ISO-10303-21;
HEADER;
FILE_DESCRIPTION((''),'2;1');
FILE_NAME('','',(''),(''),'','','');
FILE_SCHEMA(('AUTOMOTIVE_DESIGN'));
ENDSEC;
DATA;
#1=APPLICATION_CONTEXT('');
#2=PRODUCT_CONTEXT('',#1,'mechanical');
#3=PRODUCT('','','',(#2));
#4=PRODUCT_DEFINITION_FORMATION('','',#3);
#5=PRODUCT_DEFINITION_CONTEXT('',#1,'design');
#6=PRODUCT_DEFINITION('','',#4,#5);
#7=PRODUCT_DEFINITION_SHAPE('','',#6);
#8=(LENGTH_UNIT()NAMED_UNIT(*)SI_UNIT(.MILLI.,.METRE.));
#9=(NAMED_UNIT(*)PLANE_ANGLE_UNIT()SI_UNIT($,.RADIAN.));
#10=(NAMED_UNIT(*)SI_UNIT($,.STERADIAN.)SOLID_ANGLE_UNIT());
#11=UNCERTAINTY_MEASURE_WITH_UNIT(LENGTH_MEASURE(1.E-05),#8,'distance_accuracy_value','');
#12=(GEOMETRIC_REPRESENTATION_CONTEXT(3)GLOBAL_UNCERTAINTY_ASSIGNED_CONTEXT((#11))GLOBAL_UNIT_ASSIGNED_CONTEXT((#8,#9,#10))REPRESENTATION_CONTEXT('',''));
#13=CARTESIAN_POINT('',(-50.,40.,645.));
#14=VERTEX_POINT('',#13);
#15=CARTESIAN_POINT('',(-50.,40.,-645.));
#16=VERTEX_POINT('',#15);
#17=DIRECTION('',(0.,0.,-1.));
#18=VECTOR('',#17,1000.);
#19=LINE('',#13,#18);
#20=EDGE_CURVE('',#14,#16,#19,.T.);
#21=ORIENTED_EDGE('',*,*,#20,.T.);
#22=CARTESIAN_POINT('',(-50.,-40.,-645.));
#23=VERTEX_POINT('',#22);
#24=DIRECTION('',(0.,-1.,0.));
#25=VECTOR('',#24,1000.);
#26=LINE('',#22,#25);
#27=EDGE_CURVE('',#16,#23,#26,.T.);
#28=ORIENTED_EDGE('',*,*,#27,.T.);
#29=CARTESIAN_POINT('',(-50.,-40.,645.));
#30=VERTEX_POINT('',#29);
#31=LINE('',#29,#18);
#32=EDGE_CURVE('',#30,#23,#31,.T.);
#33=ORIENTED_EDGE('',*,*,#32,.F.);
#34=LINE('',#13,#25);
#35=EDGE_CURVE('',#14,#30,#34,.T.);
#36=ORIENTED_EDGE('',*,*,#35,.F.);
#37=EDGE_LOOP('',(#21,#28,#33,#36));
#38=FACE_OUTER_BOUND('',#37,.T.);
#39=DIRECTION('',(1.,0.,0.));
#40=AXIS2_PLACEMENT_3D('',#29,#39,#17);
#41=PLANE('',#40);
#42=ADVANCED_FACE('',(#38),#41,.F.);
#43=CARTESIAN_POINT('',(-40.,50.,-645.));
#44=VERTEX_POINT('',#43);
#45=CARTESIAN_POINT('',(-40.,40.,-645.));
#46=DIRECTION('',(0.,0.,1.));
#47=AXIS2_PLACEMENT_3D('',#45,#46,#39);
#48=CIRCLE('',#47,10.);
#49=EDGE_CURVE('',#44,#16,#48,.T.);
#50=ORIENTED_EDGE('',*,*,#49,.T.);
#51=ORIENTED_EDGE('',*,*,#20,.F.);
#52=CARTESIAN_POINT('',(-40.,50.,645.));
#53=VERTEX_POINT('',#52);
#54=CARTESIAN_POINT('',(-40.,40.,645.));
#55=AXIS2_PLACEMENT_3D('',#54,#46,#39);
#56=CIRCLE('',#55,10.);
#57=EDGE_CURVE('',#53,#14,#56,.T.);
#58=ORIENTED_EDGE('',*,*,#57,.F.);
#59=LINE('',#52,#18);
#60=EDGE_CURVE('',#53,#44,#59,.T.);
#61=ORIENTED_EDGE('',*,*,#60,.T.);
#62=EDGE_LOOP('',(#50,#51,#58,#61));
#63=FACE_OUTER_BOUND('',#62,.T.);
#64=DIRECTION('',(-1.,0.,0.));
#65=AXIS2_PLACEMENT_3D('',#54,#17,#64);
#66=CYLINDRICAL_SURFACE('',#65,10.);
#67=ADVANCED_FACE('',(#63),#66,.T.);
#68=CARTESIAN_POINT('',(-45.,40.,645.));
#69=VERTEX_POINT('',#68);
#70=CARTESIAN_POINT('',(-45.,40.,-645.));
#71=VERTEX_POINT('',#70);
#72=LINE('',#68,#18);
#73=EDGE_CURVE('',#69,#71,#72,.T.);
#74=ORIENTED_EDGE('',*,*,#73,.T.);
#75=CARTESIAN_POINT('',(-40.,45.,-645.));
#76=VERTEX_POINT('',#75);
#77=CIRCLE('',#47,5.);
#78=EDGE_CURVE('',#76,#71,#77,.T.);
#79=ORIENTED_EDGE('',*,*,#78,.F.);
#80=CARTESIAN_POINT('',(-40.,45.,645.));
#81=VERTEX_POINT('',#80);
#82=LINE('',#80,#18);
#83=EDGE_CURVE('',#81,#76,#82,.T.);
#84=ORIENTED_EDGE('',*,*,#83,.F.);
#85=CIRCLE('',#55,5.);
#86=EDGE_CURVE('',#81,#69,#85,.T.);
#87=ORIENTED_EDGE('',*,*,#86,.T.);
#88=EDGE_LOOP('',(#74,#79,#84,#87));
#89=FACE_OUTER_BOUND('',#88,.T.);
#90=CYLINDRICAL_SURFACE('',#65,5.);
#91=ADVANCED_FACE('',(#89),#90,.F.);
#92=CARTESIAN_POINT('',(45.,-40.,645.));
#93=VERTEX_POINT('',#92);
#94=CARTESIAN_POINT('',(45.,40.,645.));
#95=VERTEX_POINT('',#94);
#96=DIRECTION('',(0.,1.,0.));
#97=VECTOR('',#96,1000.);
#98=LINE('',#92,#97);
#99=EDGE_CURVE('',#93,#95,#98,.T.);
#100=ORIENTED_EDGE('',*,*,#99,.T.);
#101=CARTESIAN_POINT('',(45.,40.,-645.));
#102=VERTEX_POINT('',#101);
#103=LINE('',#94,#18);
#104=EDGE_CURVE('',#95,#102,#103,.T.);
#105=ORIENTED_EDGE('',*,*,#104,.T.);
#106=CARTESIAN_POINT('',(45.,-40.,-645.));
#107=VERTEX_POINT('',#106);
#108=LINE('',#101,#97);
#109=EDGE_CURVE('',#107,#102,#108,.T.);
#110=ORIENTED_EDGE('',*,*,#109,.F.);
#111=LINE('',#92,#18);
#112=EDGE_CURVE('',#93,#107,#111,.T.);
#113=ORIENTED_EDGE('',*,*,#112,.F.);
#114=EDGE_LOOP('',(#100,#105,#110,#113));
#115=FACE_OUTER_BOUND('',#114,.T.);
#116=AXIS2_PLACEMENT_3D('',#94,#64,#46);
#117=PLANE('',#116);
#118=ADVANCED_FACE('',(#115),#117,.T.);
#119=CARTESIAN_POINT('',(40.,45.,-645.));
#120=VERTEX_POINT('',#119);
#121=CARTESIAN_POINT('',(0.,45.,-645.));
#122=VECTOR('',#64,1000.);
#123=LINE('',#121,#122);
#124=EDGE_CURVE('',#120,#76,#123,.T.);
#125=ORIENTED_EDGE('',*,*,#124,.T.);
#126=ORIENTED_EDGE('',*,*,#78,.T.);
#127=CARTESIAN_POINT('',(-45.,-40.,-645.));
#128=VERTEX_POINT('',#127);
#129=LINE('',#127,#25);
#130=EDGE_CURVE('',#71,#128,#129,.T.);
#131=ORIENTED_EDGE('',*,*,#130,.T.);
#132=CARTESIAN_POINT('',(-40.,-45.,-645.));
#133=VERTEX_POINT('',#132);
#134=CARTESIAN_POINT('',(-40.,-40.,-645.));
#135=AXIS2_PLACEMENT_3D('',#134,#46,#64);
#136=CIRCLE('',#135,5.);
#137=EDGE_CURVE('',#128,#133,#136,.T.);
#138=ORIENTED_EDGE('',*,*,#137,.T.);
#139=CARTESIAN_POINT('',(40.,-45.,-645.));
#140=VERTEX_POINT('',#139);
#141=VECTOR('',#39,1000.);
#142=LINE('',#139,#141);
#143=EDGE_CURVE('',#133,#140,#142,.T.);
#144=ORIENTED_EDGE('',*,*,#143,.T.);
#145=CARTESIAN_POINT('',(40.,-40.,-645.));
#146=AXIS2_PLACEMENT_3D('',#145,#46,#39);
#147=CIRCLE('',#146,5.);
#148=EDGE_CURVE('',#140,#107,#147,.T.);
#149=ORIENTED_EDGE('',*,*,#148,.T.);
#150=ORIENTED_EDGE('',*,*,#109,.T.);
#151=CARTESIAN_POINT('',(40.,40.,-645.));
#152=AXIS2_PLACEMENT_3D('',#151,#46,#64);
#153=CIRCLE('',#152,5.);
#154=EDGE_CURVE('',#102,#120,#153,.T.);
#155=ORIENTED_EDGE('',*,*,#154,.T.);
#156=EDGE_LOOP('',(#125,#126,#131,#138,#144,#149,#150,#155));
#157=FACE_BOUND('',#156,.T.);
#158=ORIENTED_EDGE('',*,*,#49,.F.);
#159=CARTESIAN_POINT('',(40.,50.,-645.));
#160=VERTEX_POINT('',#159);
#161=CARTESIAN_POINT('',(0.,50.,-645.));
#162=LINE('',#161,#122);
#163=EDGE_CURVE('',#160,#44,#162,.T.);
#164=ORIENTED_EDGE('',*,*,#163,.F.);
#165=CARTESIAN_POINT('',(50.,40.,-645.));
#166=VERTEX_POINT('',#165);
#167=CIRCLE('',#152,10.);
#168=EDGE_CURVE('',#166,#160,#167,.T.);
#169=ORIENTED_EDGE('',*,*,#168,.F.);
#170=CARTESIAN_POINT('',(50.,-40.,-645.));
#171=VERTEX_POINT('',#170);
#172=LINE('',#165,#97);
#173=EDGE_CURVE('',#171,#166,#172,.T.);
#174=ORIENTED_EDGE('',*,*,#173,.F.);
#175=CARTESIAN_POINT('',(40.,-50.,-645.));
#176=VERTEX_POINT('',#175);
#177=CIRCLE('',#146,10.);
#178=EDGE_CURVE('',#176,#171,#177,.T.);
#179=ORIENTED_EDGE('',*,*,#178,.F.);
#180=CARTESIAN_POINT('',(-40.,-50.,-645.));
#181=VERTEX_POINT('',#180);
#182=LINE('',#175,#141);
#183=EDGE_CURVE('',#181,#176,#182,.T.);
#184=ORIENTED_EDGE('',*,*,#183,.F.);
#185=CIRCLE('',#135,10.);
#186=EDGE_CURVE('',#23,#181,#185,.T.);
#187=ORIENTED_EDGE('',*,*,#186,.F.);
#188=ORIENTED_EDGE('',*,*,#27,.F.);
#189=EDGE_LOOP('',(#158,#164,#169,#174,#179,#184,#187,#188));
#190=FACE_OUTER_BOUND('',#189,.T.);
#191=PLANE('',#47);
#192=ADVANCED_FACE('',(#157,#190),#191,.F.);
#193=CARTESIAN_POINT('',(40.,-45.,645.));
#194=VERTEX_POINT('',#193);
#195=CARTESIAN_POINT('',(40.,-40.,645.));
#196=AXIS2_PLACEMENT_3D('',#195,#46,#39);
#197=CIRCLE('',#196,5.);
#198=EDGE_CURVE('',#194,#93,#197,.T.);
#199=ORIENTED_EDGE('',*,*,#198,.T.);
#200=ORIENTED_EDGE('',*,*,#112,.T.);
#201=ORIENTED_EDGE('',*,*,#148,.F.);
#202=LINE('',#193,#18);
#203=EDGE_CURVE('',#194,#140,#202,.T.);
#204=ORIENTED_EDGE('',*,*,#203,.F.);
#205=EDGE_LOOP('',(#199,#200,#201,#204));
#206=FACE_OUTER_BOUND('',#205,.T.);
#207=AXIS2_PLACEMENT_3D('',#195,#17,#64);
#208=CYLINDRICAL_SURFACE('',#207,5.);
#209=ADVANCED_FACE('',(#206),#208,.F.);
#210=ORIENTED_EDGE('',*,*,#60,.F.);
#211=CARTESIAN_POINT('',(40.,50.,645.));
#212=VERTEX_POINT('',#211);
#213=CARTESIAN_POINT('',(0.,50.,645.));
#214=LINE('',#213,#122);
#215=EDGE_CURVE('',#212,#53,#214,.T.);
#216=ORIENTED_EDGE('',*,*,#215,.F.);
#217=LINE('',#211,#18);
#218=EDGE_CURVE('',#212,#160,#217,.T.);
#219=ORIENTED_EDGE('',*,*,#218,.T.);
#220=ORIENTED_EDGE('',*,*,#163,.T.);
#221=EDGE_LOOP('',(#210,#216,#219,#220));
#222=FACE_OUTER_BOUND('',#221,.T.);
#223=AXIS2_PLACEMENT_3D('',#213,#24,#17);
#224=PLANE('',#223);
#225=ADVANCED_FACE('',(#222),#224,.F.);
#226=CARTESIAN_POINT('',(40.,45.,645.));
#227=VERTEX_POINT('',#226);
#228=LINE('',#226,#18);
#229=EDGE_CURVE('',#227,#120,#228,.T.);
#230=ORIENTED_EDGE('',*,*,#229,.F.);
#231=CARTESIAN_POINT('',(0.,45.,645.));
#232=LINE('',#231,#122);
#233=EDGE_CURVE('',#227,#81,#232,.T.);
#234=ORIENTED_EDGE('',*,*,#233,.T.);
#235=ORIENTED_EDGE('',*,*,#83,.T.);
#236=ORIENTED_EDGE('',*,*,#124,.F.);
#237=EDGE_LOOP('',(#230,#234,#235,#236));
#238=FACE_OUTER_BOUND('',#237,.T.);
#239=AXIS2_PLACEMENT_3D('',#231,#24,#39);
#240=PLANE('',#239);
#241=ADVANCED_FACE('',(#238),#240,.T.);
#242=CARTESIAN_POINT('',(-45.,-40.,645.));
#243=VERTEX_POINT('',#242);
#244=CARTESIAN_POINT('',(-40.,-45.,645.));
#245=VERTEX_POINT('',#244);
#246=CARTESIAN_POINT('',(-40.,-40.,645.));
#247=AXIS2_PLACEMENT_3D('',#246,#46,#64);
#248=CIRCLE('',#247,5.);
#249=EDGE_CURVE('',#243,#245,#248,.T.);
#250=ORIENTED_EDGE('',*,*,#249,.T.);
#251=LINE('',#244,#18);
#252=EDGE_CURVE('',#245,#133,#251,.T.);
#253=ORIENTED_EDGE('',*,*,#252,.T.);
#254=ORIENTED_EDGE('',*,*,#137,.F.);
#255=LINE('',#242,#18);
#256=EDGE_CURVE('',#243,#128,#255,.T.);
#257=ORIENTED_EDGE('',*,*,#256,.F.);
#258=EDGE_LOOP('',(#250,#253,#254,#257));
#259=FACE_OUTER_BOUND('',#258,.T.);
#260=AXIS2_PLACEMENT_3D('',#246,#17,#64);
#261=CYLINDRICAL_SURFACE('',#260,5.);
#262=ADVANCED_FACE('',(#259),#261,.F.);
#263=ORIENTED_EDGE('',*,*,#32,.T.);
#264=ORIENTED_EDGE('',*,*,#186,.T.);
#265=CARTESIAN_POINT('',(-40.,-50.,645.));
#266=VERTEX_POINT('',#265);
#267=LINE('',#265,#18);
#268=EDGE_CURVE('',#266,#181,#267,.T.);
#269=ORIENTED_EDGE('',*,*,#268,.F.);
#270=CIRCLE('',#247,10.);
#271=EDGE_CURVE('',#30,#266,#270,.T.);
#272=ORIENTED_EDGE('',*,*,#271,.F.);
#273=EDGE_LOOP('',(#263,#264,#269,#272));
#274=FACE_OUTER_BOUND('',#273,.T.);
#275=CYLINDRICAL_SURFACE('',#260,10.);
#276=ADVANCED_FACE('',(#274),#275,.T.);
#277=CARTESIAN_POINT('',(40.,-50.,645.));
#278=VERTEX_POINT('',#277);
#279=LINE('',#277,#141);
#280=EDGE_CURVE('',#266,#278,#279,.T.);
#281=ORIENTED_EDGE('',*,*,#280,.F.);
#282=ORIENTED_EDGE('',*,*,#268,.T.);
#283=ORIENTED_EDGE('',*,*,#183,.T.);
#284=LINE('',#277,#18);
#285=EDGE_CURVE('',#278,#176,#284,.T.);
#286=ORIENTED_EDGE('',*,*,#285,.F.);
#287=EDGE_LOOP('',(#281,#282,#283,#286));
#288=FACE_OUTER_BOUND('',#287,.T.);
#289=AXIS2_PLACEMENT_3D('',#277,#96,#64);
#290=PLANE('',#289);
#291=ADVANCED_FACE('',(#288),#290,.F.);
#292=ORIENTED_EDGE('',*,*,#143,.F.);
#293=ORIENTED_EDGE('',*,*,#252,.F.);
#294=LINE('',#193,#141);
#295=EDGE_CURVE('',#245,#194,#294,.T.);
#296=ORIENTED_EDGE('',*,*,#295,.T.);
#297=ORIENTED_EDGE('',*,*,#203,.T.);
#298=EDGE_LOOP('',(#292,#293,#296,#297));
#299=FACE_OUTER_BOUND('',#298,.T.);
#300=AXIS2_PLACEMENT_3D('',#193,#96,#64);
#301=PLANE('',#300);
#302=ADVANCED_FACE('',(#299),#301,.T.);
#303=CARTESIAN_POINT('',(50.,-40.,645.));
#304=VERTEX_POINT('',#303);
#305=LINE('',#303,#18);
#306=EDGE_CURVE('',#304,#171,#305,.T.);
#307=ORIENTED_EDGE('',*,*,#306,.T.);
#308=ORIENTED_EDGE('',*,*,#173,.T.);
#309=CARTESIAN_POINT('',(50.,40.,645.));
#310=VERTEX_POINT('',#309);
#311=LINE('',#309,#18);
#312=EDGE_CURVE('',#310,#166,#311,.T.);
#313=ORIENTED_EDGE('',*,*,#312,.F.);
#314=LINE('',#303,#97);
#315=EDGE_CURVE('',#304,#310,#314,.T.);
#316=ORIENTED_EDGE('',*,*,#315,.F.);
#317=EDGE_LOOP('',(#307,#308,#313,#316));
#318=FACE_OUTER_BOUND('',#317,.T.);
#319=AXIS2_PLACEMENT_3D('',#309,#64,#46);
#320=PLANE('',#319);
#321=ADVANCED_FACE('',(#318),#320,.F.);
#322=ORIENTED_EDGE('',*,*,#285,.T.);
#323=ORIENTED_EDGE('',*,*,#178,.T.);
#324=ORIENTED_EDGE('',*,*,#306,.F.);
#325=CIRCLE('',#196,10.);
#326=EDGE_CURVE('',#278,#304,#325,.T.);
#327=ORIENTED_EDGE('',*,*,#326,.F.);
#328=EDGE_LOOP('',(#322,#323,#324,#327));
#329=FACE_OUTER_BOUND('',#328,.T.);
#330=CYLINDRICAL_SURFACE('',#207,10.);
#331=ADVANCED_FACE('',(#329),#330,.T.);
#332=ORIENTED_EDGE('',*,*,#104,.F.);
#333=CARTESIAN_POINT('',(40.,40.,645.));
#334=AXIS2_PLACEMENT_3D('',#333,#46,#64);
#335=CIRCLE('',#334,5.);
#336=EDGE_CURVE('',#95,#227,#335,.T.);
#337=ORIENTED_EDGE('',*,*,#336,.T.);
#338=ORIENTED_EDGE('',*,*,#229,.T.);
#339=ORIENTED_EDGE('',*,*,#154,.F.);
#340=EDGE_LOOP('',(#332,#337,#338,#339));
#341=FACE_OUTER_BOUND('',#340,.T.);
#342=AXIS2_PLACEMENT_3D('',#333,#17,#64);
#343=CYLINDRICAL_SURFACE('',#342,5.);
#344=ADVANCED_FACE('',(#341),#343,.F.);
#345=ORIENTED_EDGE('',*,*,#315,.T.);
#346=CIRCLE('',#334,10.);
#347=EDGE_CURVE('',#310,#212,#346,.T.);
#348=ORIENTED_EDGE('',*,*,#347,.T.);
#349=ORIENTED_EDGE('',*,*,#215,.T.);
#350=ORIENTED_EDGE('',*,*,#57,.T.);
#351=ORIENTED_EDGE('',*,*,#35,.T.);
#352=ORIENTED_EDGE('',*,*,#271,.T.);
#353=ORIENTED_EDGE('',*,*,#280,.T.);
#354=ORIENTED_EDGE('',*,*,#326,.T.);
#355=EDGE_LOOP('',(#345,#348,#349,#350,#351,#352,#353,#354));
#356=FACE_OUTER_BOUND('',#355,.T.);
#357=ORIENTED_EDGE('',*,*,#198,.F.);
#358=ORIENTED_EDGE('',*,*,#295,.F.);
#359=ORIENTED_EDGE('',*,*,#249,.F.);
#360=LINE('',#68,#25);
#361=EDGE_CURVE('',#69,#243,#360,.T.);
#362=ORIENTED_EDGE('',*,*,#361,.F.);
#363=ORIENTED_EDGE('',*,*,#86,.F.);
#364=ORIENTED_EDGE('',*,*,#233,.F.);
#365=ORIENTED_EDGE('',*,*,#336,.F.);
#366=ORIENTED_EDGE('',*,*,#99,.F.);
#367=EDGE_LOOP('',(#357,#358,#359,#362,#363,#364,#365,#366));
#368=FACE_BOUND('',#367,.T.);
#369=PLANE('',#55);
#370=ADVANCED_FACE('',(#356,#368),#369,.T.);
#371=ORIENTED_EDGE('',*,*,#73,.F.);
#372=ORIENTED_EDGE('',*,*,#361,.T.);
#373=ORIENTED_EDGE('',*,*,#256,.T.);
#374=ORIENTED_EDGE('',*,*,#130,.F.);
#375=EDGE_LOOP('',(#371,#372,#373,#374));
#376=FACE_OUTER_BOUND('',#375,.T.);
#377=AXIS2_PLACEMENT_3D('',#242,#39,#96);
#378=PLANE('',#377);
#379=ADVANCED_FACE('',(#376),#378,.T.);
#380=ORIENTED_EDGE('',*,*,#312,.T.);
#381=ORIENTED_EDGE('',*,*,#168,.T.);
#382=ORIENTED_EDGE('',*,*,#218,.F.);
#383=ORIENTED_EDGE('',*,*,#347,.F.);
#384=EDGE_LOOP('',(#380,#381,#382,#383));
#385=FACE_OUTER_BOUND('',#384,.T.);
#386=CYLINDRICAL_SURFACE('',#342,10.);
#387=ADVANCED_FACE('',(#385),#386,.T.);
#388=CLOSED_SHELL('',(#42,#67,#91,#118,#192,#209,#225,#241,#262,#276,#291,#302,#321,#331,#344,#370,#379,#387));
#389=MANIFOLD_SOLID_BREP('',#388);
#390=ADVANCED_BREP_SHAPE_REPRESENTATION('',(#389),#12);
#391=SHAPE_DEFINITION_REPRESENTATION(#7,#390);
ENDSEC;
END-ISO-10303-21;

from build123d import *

# Parameters (mm, degrees)
BOSS_EXTRUDE_1_DEPTH = 645


with BuildPart() as part:
    # Sketch 1 → Boss-Extrude 1 (new, symmetric)
    with BuildSketch(Plane.XY):
        with BuildLine():
            Line((0, 50), (-40, 50))
            ThreePointArc((-40, 50), (-47.071067812, 47.071067812), (-50, 40))
            Line((-50, 40), (-50, 0))
            Line((-50, 0), (-50, -40))
            ThreePointArc((-50, -40), (-47.071067812, -47.071067812), (-40, -50))
            Line((-40, -50), (40, -50))
            ThreePointArc((40, -50), (47.071067812, -47.071067812), (50, -40))
            Line((50, -40), (50, 0))
            Line((50, 0), (50, 40))
            ThreePointArc((50, 40), (47.071067812, 47.071067812), (40, 50))
            Line((40, 50), (0, 50))
        make_face()
        with BuildLine():
            Line((0, 45), (-40, 45))
            ThreePointArc((-40, 45), (-43.535533906, 43.535533906), (-45, 40))
            Line((-45, 40), (-45, 0))
            Line((-45, 0), (-45, -40))
            ThreePointArc((-45, -40), (-43.535533906, -43.535533906), (-40, -45))
            Line((-40, -45), (40, -45))
            ThreePointArc((40, -45), (43.535533906, -43.535533906), (45, -40))
            Line((45, -40), (45, 0))
            Line((45, 0), (45, 40))
            ThreePointArc((45, 40), (43.535533906, 43.535533906), (40, 45))
            Line((40, 45), (0, 45))
        make_face(mode=Mode.SUBTRACT)
    extrude(amount=BOSS_EXTRUDE_1_DEPTH, both=True)


solid = part.part
